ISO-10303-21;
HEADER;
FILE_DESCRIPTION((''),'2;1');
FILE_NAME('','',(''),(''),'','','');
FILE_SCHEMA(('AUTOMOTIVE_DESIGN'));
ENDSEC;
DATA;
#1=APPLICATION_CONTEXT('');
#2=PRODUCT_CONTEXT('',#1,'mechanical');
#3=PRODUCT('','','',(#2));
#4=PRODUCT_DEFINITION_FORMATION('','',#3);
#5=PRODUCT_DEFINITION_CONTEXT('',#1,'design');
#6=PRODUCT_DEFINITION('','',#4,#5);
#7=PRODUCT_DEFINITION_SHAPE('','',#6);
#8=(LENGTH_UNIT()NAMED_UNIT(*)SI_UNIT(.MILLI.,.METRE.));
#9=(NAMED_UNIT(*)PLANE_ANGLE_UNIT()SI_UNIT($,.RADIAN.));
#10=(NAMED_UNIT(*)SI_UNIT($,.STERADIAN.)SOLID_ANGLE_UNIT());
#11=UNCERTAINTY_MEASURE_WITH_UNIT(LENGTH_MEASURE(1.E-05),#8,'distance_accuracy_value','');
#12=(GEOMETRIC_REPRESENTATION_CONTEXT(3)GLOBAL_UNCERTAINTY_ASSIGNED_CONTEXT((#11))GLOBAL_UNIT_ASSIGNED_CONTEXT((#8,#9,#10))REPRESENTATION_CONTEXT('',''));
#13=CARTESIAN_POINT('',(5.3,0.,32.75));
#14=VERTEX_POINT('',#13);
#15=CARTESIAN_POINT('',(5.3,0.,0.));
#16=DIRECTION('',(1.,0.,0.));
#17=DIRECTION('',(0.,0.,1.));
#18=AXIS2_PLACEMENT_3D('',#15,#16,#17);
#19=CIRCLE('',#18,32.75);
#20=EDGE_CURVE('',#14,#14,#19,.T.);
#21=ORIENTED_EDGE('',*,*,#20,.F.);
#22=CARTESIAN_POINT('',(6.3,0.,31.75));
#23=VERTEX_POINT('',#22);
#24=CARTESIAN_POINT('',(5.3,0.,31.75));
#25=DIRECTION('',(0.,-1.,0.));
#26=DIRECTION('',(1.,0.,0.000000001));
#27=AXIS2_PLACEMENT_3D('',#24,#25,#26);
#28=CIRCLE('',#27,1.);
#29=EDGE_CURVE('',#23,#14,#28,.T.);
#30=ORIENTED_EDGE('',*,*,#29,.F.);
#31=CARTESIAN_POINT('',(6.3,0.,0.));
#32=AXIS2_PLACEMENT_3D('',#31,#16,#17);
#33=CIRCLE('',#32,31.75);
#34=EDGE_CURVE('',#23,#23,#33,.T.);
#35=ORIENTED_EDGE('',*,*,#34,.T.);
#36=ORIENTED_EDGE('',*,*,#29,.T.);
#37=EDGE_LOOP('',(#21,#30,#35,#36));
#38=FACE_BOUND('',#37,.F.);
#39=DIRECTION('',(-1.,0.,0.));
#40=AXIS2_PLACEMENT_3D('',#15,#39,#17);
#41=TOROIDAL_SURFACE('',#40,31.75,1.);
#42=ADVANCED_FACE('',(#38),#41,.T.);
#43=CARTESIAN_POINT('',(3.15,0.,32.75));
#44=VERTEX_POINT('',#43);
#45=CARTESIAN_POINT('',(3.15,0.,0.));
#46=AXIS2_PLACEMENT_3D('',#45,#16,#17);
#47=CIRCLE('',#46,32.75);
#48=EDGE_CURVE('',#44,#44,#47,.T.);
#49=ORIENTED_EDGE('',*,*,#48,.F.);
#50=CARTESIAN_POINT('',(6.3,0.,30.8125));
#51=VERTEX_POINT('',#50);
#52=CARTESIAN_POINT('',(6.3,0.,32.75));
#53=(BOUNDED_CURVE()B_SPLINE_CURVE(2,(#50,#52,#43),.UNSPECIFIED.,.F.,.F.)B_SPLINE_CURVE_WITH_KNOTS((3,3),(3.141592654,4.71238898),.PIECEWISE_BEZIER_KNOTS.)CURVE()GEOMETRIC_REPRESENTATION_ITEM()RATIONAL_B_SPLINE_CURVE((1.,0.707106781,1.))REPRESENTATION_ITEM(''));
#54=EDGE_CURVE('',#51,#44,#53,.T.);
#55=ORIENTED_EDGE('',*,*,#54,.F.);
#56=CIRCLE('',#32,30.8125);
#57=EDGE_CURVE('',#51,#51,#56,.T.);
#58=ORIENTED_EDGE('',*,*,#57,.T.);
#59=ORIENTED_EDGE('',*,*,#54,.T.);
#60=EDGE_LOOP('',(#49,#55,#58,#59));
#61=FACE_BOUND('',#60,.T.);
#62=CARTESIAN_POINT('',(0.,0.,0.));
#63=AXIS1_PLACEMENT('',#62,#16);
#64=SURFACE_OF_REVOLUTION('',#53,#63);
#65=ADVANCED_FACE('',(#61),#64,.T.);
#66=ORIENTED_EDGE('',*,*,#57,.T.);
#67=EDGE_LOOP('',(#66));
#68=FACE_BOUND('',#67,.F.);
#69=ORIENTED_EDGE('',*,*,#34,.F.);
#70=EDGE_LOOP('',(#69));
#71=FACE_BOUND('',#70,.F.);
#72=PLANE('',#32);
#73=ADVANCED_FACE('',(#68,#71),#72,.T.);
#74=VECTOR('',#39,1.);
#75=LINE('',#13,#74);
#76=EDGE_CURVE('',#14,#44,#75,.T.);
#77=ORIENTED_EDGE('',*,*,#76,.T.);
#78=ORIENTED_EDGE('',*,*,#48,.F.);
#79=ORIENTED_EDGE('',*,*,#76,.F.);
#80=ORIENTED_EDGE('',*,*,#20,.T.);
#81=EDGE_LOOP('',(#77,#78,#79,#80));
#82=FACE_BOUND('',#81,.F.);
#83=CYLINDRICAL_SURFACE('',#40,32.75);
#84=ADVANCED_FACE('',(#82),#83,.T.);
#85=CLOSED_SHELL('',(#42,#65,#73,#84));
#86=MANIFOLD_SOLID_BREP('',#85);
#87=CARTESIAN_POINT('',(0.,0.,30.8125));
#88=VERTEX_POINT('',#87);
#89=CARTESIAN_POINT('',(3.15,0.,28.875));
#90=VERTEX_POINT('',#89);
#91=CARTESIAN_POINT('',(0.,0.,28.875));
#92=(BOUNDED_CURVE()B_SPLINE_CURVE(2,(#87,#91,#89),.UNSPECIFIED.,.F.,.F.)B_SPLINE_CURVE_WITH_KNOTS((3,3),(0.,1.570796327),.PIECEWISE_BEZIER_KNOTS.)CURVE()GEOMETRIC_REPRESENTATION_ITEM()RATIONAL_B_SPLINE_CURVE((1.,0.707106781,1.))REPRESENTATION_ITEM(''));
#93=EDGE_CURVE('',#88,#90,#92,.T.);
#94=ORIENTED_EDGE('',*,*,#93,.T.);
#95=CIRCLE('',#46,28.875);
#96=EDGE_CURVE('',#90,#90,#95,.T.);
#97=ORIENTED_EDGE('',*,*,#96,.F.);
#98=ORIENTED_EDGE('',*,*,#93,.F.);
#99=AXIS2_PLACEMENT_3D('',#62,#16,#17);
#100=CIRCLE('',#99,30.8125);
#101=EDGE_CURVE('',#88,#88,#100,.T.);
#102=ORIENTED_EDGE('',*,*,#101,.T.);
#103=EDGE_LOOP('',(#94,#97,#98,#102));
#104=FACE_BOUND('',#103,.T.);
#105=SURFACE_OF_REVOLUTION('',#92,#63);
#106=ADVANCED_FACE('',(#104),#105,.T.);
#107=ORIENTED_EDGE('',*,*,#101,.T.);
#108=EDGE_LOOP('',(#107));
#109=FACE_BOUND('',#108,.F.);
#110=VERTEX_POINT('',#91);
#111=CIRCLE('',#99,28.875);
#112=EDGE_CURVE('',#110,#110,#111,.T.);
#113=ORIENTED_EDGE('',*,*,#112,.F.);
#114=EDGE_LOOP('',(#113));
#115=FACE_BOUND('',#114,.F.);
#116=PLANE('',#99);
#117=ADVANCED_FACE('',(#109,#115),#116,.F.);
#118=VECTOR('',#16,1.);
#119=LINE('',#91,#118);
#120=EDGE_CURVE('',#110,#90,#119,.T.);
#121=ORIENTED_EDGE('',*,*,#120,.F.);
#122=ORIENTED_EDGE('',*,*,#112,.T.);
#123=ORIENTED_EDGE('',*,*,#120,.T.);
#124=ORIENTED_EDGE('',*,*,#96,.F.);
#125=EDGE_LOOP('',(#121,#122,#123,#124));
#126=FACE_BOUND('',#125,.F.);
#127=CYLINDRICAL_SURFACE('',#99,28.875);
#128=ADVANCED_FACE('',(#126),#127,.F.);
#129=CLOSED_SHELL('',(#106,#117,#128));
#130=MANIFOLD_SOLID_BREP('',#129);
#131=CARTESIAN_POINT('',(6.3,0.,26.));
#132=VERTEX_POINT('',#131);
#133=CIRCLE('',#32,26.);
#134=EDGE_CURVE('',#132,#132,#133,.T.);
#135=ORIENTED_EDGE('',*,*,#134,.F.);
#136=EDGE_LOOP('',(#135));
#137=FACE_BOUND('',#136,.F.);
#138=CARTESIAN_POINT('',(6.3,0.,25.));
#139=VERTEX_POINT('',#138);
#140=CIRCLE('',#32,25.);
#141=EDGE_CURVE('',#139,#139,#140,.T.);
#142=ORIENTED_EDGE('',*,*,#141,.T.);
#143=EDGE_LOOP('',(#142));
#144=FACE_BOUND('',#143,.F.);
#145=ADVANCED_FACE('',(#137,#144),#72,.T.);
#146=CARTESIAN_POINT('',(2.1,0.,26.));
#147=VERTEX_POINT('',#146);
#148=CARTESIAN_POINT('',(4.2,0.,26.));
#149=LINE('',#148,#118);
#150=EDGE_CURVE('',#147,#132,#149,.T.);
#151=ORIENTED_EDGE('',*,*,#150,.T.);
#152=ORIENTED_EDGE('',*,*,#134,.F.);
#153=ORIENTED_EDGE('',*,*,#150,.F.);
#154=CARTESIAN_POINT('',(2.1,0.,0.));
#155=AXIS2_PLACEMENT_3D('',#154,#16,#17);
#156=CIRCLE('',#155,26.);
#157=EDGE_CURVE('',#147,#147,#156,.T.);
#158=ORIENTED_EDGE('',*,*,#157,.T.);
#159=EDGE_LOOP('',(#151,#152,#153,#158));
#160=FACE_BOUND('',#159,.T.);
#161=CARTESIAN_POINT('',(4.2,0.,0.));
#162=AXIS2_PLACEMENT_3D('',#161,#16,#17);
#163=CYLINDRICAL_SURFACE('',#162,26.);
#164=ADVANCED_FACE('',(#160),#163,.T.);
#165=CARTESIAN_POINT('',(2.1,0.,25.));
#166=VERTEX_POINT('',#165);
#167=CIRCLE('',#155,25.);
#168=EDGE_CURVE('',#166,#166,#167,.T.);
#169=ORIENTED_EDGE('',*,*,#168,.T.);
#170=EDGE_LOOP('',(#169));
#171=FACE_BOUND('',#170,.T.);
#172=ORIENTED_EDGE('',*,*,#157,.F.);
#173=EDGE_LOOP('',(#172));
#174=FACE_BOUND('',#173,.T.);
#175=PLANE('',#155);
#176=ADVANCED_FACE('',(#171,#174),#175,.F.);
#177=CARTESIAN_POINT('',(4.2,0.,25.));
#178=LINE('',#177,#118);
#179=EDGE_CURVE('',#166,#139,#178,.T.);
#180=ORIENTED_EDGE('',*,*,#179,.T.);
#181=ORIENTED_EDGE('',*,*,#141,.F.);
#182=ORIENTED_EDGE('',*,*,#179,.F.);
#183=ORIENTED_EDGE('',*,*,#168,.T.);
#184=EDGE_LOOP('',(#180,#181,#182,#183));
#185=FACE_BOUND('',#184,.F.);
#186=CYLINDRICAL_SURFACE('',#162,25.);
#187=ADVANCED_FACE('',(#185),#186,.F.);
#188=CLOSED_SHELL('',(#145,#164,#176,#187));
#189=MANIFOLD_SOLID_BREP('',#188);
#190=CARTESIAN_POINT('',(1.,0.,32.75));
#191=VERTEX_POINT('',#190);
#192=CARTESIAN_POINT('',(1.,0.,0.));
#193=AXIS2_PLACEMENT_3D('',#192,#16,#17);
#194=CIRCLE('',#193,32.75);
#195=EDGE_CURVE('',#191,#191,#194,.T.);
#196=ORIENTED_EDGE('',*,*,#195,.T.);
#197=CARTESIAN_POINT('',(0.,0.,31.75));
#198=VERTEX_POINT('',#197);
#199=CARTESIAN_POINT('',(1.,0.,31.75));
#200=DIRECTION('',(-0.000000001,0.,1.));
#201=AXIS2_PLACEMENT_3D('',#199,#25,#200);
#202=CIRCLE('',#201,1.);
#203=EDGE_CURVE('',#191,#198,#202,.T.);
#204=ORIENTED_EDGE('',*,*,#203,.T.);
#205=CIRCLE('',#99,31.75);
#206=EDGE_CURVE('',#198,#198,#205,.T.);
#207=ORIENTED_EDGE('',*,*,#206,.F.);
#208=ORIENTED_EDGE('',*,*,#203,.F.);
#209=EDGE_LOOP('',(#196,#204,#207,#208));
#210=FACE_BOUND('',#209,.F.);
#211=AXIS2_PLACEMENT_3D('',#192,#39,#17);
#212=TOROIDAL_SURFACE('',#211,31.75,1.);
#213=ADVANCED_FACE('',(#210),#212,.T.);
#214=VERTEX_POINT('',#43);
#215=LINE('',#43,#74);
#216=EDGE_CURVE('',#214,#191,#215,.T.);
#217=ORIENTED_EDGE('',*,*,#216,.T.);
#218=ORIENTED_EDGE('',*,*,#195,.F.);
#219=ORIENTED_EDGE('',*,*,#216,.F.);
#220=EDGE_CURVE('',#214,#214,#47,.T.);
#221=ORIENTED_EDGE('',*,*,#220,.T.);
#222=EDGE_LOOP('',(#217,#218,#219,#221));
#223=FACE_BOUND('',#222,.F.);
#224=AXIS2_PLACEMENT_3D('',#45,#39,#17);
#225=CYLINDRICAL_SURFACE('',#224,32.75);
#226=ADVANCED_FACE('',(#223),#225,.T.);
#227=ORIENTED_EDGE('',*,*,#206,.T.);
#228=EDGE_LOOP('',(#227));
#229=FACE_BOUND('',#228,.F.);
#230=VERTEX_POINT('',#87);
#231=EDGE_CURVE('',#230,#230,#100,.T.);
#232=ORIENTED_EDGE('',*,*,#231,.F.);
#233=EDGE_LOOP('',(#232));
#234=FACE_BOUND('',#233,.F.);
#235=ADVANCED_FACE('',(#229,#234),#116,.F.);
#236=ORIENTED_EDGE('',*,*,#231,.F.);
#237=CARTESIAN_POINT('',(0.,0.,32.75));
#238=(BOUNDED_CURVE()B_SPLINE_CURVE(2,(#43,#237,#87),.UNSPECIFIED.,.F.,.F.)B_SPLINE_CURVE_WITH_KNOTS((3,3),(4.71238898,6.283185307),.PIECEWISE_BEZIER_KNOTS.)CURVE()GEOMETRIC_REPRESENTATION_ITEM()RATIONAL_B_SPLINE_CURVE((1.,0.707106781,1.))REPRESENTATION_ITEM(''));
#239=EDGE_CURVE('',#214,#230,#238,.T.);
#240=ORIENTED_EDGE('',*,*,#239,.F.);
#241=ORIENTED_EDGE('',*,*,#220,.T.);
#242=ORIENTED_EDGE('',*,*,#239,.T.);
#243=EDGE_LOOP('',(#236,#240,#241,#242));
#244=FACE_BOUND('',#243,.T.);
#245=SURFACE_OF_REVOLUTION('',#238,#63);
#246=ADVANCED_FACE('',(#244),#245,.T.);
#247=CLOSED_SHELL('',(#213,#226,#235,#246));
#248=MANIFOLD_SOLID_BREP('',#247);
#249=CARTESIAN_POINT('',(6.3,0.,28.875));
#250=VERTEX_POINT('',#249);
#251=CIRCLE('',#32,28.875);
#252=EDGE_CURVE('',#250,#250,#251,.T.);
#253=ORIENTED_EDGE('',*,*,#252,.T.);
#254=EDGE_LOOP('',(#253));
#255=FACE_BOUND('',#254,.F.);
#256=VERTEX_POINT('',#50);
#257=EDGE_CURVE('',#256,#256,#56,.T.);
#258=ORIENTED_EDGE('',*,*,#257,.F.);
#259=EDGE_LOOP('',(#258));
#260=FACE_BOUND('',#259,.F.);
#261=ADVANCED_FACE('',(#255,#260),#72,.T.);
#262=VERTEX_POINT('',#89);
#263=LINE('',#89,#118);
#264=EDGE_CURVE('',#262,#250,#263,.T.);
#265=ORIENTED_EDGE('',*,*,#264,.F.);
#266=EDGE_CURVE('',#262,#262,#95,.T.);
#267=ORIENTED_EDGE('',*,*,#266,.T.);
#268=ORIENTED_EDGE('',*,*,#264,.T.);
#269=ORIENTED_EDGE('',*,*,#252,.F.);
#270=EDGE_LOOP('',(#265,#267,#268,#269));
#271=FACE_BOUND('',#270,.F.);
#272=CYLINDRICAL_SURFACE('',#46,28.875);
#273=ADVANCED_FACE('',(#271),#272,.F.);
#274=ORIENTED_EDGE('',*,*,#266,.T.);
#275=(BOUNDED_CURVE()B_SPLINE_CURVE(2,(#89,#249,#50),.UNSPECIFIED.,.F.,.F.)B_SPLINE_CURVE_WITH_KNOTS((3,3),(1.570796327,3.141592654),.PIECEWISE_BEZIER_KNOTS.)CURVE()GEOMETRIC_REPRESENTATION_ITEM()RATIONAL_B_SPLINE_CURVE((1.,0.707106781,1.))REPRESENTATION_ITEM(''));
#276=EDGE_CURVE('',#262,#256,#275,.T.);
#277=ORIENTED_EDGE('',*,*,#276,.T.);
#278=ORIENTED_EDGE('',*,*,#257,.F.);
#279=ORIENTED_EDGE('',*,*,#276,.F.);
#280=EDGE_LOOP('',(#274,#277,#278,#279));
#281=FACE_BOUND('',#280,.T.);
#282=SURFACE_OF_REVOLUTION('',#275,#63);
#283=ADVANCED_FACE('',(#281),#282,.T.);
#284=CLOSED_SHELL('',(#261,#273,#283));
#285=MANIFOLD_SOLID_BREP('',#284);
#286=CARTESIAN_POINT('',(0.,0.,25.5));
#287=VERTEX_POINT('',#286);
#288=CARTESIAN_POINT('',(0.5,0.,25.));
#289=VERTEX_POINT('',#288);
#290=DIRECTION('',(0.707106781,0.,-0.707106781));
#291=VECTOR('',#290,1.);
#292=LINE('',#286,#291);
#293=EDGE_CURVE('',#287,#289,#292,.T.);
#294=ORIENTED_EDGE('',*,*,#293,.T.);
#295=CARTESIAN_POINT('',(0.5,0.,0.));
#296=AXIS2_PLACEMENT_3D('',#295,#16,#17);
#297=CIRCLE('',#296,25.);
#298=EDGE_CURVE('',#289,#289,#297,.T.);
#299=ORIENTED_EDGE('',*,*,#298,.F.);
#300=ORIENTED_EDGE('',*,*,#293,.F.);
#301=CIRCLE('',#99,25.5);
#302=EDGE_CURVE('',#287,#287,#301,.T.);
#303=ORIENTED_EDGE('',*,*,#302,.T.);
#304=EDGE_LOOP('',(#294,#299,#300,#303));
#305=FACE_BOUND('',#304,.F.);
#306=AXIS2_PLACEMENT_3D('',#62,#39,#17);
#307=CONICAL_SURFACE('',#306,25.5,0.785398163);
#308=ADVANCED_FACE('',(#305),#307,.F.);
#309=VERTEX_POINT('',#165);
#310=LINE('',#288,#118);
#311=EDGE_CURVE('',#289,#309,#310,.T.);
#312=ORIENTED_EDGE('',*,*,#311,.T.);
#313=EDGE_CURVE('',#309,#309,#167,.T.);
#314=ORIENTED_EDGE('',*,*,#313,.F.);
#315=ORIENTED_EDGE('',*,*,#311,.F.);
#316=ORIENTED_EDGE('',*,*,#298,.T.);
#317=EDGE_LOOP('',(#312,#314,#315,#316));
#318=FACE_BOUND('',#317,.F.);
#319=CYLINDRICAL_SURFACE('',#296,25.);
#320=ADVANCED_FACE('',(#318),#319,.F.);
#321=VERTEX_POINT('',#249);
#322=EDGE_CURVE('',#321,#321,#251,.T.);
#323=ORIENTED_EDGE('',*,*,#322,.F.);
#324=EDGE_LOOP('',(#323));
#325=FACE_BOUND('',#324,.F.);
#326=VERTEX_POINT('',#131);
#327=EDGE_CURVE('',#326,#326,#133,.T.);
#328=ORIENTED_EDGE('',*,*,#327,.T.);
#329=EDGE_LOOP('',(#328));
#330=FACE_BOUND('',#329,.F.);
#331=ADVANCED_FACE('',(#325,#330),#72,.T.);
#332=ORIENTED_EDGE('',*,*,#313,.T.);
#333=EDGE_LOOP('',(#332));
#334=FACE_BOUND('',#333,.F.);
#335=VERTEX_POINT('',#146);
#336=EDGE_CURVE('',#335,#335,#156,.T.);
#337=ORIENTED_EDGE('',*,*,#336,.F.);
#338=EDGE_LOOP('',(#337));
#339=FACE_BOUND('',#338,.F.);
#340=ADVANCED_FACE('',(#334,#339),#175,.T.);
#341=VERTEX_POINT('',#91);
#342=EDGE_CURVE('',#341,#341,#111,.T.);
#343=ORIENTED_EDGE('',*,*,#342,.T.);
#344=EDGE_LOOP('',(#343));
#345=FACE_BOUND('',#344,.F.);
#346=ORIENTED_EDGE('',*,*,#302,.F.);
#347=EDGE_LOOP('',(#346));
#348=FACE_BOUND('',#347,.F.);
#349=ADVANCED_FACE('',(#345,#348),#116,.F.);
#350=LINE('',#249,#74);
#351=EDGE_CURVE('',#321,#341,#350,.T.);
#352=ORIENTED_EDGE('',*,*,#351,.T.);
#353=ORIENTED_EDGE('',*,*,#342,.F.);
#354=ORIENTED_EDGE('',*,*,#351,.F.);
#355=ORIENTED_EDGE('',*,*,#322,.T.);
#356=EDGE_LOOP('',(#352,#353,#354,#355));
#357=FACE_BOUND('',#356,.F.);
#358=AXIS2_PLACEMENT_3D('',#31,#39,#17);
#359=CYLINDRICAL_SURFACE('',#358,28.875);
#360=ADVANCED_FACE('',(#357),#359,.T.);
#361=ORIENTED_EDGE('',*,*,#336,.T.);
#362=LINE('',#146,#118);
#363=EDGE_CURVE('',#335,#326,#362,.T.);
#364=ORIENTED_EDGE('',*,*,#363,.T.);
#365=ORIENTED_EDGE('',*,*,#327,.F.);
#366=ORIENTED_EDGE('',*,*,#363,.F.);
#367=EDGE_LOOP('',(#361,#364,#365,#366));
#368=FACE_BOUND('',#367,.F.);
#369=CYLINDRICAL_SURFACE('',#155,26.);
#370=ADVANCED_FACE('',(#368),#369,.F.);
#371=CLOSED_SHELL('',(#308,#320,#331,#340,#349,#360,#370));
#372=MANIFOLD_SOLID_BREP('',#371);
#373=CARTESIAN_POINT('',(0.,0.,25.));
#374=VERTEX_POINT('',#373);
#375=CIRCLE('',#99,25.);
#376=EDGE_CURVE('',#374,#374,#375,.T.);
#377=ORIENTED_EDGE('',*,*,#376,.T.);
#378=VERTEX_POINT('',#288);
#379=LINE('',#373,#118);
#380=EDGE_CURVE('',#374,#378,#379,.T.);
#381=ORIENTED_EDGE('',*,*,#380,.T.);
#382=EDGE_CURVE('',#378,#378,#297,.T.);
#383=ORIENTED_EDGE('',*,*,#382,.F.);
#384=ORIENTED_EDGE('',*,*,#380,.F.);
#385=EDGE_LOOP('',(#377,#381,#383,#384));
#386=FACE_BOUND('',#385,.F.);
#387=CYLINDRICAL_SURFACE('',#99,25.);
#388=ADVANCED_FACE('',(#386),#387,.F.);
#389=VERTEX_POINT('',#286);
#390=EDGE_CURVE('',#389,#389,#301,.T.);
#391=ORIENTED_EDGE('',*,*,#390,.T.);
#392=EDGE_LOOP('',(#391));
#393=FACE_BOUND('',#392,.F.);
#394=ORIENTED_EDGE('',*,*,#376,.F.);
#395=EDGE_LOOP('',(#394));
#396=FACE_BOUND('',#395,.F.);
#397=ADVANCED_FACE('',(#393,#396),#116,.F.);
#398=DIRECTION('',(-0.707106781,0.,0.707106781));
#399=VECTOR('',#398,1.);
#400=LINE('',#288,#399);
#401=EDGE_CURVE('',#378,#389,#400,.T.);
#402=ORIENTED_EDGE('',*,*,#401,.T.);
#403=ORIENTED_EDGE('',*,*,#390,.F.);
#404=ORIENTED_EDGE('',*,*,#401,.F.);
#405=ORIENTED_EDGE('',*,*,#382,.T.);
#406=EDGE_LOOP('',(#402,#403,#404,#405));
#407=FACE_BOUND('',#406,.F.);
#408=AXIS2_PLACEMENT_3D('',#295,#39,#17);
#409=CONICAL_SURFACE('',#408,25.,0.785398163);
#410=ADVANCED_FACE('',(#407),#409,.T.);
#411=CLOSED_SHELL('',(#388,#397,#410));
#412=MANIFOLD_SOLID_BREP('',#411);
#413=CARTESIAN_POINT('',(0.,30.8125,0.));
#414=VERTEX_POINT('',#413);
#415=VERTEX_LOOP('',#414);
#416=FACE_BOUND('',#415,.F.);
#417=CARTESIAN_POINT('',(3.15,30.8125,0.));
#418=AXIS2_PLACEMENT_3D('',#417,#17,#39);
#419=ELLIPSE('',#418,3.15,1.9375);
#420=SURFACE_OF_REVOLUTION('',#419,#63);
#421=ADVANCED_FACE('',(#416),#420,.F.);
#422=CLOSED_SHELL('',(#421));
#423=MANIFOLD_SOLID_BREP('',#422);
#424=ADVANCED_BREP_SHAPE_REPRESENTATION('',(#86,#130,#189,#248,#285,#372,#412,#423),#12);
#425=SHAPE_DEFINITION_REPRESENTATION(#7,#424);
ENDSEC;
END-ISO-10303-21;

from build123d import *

# Parameters (mm, degrees)
SKETCH_1_3_RX = 3.15
SKETCH_1_3_RY = 1.9375
SKETCH_1_4_W  = 4.2
SKETCH_1_4_H  = 1


with BuildPart() as part:
    # 草图1 → 旋转1 (revolve)
    with BuildSketch(Plane.XY, mode=Mode.PRIVATE) as revolve_1_sk:
        Polygon((3.15, 28.875), (0, 28.875), (0, 25.5), (0.5, 25), (2.1, 25), (2.1, 26), (6.3, 26), (6.3, 28.875), align=None)
    revolve(revolve_1_sk.sketch.rotate(Axis((0, 0, 0), (1, 0, 0)), 90), axis=Axis((0, 0, 0), (1, 0, 0)))


with BuildPart() as body_2:
    # 草图1<3> → 旋转2 (revolve)
    with BuildSketch(Plane.XY):
        with Locations(Location((3.15, 30.8125), (0, 0, 180))):
            Ellipse(SKETCH_1_3_RX, SKETCH_1_3_RY)
    revolve(axis=Axis((0, 0, 0), (1, 0, 0)))


with BuildPart() as body_3:
    # 草图1<4> → 旋转3 (revolve)
    with BuildSketch(Plane.XY, mode=Mode.PRIVATE) as revolve_3_sk:
        with BuildLine():
            Line((0, 30.8125), (0, 28.875))
            Line((0, 28.875), (3.15, 28.875))
            add(Edge.make_bspline(
                [(0, 30.8125), (0, 28.875), (3.15, 28.875)],
                knots=[0, 0, 0, 1.570796327, 1.570796327, 1.570796327], degree=2, weights=[1, 0.707106781, 1]))
        make_face()
        with BuildLine():
            add(Edge.make_bspline(
                [(3.15, 28.875), (6.3, 28.875), (6.3, 30.8125)],
                knots=[1.570796327, 1.570796327, 1.570796327, 3.141592654, 3.141592654, 3.141592654], degree=2, weights=[1, 0.707106781, 1]))
            Line((3.15, 28.875), (6.3, 28.875))
            Line((6.3, 28.875), (6.3, 30.8125))
        make_face()
        Polygon((0.5, 25), (0, 25.5), (0, 25), align=None)
        with BuildLine():
            Line((0, 31.75), (0, 30.8125))
            add(Edge.make_bspline(
                [(3.15, 32.75), (0, 32.75), (0, 30.8125)],
                knots=[4.71238898, 4.71238898, 4.71238898, 6.283185307, 6.283185307, 6.283185307], degree=2, weights=[1, 0.707106781, 1]))
            Line((3.15, 32.75), (1, 32.75))
            ThreePointArc((1, 32.75), (0.292893219, 32.457106781), (0, 31.75))
        make_face()
        with BuildLine():
            add(Edge.make_bspline(
                [(6.3, 30.8125), (6.3, 32.75), (3.15, 32.75)],
                knots=[3.141592654, 3.141592654, 3.141592654, 4.71238898, 4.71238898, 4.71238898], degree=2, weights=[1, 0.707106781, 1]))
            Line((6.3, 30.8125), (6.3, 31.75))
            ThreePointArc((6.3, 31.75), (6.007106781, 32.457106781), (5.3, 32.75))
            Line((5.3, 32.75), (3.15, 32.75))
        make_face()
        with Locations((4.2, 25.5)):
            Rectangle(SKETCH_1_4_W, SKETCH_1_4_H)
    revolve(revolve_3_sk.sketch.rotate(Axis((0, 0, 0), (1, 0, 0)), 90), axis=Axis((0, 0, 0), (1, 0, 0)))


solid = Compound([part.part, body_2.part, body_3.part])
